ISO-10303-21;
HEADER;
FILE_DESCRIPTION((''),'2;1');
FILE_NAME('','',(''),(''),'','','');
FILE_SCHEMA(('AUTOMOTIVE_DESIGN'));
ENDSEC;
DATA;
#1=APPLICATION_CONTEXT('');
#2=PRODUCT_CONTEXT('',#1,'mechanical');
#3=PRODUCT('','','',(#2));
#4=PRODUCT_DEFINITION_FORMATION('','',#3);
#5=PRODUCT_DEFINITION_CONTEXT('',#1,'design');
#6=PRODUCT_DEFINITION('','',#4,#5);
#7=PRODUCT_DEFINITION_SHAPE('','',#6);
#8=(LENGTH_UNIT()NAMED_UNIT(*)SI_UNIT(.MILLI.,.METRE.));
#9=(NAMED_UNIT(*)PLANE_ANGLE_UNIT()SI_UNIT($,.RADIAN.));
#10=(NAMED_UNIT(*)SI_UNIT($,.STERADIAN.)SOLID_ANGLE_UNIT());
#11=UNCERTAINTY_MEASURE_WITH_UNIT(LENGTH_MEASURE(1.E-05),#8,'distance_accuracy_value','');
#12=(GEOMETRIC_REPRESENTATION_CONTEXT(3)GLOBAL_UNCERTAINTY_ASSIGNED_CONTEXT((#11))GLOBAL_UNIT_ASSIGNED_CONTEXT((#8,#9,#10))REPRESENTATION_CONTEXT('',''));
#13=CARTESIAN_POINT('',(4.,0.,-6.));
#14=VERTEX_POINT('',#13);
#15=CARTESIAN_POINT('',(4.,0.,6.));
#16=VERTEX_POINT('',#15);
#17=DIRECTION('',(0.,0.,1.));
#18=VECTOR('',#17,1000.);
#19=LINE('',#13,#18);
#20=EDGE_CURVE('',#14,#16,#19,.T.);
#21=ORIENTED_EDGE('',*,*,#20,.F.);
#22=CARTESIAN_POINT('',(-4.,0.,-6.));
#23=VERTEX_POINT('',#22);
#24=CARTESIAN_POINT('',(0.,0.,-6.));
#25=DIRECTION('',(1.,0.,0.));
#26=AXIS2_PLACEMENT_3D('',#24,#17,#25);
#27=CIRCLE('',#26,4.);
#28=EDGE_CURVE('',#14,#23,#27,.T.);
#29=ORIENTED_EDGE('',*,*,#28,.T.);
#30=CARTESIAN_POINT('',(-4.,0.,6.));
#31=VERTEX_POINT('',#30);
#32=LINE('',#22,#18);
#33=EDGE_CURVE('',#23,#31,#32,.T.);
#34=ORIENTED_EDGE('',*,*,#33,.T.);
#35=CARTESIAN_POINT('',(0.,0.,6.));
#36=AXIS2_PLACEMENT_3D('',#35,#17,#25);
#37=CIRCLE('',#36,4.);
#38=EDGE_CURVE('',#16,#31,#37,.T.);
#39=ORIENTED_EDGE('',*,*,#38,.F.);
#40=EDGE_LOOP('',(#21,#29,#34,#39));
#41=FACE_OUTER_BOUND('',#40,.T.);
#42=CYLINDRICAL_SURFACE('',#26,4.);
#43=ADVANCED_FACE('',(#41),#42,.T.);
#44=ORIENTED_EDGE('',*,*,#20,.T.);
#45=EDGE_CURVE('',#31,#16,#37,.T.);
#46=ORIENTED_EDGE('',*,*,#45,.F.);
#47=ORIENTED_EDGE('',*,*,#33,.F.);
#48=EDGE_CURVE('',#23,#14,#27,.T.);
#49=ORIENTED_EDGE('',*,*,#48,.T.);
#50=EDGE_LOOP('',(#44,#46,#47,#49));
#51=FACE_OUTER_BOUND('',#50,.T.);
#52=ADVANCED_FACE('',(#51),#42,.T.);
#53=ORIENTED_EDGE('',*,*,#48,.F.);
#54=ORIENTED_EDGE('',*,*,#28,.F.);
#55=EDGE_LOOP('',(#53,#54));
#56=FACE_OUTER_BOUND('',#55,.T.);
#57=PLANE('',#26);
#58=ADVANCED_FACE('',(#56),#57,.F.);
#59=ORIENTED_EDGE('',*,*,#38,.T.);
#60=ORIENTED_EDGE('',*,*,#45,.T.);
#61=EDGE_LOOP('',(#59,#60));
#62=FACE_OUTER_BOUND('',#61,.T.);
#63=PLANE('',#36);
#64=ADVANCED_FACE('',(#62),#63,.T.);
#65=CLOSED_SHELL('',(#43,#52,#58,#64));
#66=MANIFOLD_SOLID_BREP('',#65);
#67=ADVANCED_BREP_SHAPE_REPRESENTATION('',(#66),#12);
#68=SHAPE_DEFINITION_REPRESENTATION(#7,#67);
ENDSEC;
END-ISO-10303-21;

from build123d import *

# Parameters (mm, degrees)
SKETCH_1_R      = 4
EXTRUDE_1_DEPTH = 6


with BuildPart() as part:
    # 草图1 → 凸台-拉伸1 (new, symmetric)
    with BuildSketch(Plane.XY):
        Circle(SKETCH_1_R)
    extrude(amount=EXTRUDE_1_DEPTH, both=True)


solid = part.part
